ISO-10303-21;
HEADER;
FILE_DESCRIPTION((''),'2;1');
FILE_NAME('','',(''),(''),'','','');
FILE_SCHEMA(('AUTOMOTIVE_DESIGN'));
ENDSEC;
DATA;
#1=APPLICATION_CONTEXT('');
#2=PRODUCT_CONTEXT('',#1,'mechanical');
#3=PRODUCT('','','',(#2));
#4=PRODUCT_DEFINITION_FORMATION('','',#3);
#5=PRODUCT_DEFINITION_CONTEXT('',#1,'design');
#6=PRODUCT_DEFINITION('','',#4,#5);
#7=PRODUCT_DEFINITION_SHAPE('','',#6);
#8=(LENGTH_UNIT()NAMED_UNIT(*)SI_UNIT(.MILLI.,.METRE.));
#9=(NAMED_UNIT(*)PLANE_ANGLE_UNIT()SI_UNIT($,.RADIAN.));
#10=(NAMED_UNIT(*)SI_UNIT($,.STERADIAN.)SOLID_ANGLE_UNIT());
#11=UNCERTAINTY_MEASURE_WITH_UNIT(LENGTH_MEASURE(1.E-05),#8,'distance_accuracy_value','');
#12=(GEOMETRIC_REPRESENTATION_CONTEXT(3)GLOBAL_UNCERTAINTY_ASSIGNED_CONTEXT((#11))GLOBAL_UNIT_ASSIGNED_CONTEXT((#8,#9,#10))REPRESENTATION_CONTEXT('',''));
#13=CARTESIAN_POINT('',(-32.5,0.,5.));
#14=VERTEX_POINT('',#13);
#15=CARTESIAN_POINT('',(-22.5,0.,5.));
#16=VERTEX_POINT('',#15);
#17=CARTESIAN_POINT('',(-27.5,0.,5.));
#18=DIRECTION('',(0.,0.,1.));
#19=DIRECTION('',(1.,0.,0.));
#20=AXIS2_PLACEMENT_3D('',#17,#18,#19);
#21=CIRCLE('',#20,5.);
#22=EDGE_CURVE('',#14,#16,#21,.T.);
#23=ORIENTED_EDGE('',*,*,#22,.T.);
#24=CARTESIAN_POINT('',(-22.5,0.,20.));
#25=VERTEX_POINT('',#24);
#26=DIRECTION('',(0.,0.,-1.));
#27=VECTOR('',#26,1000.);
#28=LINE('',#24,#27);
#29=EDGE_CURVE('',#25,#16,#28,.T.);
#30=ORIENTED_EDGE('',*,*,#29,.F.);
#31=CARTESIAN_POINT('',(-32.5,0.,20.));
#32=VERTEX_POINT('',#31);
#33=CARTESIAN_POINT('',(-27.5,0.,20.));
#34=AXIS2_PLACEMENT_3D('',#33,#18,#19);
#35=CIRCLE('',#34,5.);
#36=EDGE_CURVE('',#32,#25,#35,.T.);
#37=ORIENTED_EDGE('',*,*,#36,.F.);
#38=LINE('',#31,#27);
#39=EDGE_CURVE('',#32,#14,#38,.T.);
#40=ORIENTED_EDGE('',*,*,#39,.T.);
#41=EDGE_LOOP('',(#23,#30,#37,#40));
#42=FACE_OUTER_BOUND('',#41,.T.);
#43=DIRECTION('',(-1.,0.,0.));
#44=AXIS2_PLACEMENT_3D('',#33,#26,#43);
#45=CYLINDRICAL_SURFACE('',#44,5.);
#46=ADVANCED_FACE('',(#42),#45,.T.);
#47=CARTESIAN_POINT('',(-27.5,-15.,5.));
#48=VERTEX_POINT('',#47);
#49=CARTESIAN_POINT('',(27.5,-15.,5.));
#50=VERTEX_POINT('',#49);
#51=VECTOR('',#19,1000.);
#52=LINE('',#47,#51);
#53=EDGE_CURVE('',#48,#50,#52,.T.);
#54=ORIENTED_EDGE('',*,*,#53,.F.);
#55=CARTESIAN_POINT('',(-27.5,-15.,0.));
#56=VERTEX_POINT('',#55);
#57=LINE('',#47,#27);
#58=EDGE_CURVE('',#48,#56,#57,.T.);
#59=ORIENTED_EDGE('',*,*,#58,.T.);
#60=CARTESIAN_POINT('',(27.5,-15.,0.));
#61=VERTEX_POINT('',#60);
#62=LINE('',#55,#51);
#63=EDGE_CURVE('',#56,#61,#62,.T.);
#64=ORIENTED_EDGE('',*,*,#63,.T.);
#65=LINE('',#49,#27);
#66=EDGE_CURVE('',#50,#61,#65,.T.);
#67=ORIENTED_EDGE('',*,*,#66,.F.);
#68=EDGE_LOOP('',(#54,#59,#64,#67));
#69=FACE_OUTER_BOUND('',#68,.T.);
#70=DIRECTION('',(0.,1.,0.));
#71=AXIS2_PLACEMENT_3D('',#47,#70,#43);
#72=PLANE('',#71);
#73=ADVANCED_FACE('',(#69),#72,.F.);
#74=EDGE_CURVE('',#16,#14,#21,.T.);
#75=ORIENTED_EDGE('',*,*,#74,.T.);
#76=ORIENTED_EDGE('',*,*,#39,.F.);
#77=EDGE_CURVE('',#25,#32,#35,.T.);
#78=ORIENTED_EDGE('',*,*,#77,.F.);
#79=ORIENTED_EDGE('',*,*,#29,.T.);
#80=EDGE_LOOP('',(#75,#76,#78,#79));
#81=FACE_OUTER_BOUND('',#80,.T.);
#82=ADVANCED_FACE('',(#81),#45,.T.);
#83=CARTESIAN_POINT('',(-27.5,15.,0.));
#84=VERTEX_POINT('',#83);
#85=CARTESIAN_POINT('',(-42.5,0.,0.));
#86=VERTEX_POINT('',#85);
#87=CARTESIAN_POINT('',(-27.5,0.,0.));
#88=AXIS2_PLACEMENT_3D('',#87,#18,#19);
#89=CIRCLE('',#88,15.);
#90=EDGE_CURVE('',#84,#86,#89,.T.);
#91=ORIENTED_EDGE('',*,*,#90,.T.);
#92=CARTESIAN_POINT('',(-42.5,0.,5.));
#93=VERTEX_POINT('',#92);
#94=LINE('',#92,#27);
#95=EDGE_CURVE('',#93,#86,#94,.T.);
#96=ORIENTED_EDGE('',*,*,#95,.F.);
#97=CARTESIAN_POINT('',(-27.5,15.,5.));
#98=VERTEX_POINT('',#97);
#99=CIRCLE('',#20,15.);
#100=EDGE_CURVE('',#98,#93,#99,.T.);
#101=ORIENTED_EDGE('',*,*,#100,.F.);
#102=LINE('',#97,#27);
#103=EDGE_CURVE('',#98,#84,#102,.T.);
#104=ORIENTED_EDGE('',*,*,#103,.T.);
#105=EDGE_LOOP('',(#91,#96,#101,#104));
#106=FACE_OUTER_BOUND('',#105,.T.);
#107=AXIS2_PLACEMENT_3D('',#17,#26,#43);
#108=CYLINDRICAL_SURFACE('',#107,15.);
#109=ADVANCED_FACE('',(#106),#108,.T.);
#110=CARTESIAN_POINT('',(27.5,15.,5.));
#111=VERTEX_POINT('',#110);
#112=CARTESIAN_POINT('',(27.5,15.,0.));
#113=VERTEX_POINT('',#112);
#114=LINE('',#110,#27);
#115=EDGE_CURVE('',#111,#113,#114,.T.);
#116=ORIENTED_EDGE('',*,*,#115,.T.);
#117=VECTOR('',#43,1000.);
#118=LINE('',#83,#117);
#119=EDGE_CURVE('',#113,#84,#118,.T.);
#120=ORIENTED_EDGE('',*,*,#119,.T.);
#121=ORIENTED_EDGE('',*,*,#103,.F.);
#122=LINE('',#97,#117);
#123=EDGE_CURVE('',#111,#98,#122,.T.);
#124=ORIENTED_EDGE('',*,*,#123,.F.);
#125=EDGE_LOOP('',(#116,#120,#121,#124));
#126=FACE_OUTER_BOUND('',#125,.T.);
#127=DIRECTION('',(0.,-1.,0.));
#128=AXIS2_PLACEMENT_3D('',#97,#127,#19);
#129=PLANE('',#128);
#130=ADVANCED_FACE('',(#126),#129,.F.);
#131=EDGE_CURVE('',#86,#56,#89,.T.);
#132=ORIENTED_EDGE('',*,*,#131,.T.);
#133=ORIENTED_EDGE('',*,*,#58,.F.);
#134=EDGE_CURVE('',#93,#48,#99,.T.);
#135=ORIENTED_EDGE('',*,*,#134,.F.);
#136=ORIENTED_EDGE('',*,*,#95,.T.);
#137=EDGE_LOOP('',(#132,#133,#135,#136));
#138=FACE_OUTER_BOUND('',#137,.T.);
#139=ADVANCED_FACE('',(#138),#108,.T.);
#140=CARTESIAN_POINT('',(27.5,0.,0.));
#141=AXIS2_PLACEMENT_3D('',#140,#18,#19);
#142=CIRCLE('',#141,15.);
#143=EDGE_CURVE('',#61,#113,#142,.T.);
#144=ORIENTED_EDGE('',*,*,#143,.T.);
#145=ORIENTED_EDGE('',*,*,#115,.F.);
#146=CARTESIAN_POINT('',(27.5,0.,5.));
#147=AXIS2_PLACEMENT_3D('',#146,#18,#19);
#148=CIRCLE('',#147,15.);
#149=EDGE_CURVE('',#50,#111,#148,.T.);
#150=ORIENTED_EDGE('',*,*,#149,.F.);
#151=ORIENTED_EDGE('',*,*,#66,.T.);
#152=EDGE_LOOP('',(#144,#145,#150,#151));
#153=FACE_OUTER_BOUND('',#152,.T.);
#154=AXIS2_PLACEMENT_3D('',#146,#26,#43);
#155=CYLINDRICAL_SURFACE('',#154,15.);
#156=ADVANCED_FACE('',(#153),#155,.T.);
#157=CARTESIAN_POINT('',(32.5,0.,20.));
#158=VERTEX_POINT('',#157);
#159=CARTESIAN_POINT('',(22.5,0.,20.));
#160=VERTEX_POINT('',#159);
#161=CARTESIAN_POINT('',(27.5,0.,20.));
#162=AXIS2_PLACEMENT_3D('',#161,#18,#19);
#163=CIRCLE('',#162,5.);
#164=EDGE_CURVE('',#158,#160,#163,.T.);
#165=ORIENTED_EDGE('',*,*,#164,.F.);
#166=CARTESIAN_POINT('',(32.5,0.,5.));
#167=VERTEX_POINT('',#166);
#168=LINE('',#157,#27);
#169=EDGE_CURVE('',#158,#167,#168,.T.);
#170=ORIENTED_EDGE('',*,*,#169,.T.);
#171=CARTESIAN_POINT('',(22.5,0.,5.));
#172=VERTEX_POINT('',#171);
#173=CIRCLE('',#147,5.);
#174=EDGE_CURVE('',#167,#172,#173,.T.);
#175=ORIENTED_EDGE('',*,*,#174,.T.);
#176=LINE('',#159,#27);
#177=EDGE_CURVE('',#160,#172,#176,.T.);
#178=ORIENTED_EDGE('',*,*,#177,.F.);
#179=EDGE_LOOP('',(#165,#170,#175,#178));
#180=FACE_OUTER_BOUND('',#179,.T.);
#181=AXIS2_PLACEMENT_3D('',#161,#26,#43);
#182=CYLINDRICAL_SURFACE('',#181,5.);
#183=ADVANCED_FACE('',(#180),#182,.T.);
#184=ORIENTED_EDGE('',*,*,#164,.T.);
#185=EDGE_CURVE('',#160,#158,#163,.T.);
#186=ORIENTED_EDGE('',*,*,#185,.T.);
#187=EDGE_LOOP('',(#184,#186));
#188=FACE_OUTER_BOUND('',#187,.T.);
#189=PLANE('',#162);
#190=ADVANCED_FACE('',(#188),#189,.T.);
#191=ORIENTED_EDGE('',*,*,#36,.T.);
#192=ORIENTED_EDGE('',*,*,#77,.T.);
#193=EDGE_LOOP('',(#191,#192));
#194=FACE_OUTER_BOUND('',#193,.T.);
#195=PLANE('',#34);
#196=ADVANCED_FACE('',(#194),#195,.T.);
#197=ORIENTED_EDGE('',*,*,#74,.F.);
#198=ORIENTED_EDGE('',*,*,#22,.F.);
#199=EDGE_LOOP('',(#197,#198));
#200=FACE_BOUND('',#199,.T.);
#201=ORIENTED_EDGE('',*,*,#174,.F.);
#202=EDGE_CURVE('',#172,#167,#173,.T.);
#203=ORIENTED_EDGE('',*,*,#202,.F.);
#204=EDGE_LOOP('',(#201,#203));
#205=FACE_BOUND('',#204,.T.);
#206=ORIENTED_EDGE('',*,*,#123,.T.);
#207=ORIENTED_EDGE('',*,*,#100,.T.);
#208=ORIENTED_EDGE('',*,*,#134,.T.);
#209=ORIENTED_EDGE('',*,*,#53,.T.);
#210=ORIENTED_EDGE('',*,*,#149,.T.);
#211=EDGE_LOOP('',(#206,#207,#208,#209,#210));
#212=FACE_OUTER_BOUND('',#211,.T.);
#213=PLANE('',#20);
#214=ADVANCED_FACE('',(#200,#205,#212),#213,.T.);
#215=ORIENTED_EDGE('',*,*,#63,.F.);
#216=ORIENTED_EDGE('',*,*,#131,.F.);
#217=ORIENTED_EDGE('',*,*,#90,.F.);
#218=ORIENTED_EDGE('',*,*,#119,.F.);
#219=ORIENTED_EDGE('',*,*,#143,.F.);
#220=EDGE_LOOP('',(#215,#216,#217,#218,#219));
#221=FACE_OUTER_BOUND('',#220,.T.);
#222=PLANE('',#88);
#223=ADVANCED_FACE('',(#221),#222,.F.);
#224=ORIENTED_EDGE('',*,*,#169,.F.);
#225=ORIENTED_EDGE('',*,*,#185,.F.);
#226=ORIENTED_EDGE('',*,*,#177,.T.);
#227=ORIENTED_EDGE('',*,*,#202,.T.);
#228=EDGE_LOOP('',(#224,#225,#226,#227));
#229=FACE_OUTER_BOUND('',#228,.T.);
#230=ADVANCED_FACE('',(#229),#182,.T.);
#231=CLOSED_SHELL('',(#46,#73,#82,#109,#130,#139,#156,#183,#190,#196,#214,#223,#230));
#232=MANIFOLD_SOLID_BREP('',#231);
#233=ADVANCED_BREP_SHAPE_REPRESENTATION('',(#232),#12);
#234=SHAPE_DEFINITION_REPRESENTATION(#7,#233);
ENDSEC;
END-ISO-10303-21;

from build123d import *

# Parameters (mm, degrees)
BASE_PLATE_DEPTH     = 5
PIN_CIRCLES_SKETCH_R = 5
PINS_2X_10_DEPTH     = 15


with BuildPart() as part:
    # Plate Outline Sketch → Base Plate (new body)
    with BuildSketch(Plane.XY):
        with BuildLine():
            Line((-27.5, 15), (27.5, 15))
            ThreePointArc((27.5, 15), (42.5, 0), (27.5, -15))
            Line((27.5, -15), (-27.5, -15))
            ThreePointArc((-27.5, -15), (-42.5, 0), (-27.5, 15))
        make_face()
    extrude(amount=BASE_PLATE_DEPTH)

    # Pin Circles Sketch → Pins 2xØ10 (add)
    with BuildSketch(Plane.XY.offset(5)):
        with Locations((-27.5, 0)):
            Circle(PIN_CIRCLES_SKETCH_R)
        with Locations((27.5, 0)):
            Circle(PIN_CIRCLES_SKETCH_R)
    extrude(amount=PINS_2X_10_DEPTH)


solid = part.part
